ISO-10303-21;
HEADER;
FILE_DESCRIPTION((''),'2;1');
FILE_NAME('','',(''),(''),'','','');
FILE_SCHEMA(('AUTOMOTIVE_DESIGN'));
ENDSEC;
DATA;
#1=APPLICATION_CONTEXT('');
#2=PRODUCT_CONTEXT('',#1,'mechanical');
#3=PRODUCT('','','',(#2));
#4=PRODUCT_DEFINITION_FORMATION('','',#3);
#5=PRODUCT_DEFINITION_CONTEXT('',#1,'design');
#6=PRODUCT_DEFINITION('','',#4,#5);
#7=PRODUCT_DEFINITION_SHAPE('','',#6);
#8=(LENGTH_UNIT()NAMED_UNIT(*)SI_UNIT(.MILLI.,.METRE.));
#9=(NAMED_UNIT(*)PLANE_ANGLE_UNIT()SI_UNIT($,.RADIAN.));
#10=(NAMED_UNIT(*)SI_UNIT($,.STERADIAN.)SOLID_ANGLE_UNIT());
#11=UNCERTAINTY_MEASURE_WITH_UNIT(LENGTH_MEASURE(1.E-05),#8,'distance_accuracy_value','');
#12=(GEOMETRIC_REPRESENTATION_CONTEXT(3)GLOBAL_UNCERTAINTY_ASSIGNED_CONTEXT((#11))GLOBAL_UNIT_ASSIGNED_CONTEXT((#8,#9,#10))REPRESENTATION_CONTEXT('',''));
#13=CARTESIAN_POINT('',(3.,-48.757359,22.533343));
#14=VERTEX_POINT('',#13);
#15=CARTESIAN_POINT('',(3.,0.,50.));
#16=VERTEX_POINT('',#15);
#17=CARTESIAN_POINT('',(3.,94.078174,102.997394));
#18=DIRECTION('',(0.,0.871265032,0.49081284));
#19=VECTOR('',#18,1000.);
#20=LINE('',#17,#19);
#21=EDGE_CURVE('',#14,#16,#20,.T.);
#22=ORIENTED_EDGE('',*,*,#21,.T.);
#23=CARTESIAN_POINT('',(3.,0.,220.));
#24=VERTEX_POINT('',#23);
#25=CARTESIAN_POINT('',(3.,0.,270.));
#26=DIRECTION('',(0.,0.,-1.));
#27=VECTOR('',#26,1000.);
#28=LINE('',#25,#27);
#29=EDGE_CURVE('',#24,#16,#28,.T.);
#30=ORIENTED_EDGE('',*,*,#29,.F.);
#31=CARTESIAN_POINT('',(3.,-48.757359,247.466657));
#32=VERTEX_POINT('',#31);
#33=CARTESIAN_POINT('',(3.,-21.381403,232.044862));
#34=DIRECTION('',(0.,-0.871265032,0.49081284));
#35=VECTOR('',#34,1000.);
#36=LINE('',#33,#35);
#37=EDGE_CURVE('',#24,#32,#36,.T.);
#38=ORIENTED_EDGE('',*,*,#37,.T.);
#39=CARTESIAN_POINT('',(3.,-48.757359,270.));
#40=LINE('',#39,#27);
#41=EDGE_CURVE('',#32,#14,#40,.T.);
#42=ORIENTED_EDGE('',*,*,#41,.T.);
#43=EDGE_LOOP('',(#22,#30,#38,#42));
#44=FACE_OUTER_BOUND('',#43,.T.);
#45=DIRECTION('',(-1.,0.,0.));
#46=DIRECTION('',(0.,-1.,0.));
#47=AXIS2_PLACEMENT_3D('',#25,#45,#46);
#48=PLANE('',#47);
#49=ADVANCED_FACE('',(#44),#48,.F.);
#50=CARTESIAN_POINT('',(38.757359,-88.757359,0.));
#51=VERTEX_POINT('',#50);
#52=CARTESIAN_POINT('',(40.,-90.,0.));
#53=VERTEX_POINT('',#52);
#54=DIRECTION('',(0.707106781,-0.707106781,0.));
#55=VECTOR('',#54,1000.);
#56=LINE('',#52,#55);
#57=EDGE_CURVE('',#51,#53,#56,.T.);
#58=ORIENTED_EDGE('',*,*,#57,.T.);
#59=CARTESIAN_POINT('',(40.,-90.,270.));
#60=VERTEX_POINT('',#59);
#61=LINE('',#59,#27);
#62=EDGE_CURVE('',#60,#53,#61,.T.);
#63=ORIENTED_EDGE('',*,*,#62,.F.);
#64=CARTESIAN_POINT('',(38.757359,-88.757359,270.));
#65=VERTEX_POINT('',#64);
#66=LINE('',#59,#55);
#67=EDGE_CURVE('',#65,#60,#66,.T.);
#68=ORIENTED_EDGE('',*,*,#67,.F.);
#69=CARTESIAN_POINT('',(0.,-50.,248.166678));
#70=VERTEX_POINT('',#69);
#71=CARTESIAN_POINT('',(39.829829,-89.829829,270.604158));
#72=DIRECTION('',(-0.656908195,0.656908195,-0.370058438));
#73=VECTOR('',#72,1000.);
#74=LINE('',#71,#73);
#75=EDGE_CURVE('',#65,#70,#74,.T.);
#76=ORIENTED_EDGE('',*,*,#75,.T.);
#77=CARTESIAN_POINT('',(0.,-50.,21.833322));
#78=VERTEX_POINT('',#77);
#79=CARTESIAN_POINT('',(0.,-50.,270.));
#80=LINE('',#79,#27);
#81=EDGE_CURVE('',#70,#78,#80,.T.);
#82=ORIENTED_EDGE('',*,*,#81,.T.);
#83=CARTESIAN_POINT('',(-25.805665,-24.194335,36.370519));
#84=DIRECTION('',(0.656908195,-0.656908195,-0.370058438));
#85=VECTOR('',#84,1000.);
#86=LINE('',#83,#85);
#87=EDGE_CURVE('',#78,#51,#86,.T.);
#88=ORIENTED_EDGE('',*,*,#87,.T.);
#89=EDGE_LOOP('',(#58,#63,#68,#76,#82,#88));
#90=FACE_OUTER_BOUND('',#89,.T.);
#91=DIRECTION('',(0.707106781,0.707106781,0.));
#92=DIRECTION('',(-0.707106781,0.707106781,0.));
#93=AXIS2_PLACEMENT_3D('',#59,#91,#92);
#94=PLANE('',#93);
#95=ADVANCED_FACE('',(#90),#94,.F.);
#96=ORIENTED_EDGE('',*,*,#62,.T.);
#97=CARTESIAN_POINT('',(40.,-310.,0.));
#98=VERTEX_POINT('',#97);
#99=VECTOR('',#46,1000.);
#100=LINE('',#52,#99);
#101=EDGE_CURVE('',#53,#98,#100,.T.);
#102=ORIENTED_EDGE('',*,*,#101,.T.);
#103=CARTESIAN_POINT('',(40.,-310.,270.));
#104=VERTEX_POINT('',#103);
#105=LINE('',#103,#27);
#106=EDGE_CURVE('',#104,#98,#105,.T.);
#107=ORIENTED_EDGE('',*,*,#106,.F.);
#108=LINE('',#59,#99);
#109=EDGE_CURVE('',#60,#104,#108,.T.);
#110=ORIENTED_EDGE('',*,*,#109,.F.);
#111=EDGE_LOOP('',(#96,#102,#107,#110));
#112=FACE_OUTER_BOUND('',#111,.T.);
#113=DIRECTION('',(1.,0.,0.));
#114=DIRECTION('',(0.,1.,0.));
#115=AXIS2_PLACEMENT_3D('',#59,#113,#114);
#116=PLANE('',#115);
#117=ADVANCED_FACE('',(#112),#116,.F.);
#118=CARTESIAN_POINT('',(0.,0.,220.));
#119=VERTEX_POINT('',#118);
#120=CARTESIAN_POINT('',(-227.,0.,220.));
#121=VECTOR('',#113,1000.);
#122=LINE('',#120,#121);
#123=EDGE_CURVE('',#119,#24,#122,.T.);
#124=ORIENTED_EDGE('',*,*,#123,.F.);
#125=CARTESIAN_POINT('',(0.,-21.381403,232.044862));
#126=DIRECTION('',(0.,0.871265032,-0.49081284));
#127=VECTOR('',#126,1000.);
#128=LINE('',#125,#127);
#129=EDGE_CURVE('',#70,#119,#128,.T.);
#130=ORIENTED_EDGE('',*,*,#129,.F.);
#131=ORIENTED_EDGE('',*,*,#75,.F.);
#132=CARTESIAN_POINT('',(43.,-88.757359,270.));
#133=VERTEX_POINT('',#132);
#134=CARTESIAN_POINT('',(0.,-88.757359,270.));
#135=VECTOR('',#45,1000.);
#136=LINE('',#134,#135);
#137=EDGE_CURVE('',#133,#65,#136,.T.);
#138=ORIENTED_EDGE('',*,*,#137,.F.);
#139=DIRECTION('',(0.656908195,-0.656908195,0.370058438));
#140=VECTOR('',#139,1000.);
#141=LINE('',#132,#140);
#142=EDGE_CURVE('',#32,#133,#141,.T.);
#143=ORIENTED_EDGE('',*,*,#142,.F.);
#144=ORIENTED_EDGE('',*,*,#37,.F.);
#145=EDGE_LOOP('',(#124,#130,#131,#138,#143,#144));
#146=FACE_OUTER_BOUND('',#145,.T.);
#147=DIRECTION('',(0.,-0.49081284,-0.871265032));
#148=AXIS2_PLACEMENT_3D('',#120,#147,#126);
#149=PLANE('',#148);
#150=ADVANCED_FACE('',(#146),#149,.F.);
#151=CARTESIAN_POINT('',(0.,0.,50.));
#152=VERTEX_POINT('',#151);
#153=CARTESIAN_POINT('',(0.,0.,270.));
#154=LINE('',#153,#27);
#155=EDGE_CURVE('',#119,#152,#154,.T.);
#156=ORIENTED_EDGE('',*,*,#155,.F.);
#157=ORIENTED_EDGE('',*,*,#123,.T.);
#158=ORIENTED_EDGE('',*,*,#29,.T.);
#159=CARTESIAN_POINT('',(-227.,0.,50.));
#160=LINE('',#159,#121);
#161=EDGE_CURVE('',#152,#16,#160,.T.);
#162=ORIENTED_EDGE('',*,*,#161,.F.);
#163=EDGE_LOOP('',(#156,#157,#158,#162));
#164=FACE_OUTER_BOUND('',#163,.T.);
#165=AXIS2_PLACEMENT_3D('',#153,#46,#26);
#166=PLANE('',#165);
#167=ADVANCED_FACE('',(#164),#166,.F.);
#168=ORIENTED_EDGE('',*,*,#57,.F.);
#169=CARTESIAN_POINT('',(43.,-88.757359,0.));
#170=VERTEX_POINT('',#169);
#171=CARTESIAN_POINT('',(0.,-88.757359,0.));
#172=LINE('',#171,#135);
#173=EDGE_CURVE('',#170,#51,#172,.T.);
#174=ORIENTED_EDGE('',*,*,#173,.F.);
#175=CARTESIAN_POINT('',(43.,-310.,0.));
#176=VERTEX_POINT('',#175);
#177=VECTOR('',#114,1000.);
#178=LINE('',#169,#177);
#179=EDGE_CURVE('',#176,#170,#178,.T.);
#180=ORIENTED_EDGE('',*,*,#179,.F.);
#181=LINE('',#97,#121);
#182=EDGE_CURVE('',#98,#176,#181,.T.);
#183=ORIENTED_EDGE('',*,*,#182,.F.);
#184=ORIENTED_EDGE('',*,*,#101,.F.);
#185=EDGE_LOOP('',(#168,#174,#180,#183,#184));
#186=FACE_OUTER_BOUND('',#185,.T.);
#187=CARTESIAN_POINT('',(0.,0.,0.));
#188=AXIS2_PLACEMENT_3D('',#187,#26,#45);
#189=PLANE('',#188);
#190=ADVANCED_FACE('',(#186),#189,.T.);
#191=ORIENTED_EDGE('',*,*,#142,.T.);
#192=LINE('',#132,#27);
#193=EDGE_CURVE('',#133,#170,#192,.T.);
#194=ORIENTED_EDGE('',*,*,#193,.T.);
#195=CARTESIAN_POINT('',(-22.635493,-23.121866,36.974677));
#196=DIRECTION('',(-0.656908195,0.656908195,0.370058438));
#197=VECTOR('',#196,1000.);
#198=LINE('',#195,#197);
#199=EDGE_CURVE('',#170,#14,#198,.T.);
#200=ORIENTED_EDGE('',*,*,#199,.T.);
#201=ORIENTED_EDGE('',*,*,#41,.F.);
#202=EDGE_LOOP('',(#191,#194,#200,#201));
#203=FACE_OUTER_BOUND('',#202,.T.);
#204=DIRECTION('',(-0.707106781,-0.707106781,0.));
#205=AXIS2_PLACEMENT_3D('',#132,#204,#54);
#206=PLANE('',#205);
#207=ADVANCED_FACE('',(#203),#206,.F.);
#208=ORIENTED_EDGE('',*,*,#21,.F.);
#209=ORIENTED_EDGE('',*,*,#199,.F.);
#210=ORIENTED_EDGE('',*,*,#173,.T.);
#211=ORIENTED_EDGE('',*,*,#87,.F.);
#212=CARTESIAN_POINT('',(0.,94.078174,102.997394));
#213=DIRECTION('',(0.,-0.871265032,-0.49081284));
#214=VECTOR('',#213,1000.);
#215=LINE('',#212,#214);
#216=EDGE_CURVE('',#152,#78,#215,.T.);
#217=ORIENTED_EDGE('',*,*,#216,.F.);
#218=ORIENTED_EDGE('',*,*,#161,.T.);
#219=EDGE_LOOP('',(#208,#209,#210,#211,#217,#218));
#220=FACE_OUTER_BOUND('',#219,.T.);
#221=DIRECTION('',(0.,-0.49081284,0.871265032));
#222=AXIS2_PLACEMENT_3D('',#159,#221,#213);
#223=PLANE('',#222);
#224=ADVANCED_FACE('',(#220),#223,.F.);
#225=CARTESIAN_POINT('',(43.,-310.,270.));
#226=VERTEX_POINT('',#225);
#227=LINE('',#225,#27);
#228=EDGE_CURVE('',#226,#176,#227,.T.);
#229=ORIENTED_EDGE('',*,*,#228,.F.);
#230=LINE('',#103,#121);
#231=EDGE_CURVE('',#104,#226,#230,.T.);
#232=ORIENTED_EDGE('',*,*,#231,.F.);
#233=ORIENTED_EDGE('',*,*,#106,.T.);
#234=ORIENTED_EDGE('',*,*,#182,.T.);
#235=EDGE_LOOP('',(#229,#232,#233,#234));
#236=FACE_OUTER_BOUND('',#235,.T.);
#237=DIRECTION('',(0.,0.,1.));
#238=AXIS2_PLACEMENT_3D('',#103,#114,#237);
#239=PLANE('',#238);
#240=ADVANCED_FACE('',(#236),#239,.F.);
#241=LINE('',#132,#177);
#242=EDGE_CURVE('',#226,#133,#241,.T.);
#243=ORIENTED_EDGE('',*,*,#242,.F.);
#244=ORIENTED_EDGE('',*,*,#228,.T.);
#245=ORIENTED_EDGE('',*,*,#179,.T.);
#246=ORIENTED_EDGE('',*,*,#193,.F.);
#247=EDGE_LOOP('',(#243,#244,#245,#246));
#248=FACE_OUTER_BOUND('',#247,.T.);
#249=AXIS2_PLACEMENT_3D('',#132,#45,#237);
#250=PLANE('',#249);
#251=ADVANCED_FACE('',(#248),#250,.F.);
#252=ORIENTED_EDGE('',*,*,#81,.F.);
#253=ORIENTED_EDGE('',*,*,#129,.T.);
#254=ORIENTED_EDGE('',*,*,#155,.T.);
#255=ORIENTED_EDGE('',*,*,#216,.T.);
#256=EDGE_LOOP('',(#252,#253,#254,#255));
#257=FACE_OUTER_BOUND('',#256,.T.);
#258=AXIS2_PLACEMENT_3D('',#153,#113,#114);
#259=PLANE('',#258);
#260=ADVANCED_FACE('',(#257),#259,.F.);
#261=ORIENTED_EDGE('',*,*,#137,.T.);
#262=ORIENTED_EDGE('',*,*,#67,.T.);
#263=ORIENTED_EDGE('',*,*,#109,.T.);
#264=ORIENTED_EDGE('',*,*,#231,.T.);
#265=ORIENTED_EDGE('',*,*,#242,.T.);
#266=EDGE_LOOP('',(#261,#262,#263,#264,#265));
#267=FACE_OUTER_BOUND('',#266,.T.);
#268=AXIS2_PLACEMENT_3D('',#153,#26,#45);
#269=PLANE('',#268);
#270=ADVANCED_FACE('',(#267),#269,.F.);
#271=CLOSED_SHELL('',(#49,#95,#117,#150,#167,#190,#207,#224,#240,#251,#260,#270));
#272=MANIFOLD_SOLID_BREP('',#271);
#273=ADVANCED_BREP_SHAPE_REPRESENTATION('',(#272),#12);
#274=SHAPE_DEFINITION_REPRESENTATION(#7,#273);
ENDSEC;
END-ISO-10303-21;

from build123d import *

# Parameters (mm, degrees)
EXTRUDE_1_DEPTH     = 270
CUT_EXTRUDE_2_DEPTH = 270


with BuildPart() as part:
    # 草图1 → 凸台-拉伸1 (new body)
    with BuildSketch(Plane.XY):
        Polygon((0, 0), (0, -50), (40, -90), (40, -310), (43, -310), (43, -88.757359313), (3, -48.757359313), (3, 0), align=None)
    extrude(amount=EXTRUDE_1_DEPTH)

    # 草图2 → 切除-拉伸2 (cut)
    with BuildSketch(Plane(origin=(43, 0, 0), x_dir=(0, 0, -1), z_dir=(1, 0, 0))):
        Polygon((-270, 0), (-220, 0), (-270, -88.757359313), align=None)
        Polygon((0, 0), (-50, 0), (0, -88.757359313), align=None)
    extrude(amount=-CUT_EXTRUDE_2_DEPTH, mode=Mode.SUBTRACT)


solid = part.part
